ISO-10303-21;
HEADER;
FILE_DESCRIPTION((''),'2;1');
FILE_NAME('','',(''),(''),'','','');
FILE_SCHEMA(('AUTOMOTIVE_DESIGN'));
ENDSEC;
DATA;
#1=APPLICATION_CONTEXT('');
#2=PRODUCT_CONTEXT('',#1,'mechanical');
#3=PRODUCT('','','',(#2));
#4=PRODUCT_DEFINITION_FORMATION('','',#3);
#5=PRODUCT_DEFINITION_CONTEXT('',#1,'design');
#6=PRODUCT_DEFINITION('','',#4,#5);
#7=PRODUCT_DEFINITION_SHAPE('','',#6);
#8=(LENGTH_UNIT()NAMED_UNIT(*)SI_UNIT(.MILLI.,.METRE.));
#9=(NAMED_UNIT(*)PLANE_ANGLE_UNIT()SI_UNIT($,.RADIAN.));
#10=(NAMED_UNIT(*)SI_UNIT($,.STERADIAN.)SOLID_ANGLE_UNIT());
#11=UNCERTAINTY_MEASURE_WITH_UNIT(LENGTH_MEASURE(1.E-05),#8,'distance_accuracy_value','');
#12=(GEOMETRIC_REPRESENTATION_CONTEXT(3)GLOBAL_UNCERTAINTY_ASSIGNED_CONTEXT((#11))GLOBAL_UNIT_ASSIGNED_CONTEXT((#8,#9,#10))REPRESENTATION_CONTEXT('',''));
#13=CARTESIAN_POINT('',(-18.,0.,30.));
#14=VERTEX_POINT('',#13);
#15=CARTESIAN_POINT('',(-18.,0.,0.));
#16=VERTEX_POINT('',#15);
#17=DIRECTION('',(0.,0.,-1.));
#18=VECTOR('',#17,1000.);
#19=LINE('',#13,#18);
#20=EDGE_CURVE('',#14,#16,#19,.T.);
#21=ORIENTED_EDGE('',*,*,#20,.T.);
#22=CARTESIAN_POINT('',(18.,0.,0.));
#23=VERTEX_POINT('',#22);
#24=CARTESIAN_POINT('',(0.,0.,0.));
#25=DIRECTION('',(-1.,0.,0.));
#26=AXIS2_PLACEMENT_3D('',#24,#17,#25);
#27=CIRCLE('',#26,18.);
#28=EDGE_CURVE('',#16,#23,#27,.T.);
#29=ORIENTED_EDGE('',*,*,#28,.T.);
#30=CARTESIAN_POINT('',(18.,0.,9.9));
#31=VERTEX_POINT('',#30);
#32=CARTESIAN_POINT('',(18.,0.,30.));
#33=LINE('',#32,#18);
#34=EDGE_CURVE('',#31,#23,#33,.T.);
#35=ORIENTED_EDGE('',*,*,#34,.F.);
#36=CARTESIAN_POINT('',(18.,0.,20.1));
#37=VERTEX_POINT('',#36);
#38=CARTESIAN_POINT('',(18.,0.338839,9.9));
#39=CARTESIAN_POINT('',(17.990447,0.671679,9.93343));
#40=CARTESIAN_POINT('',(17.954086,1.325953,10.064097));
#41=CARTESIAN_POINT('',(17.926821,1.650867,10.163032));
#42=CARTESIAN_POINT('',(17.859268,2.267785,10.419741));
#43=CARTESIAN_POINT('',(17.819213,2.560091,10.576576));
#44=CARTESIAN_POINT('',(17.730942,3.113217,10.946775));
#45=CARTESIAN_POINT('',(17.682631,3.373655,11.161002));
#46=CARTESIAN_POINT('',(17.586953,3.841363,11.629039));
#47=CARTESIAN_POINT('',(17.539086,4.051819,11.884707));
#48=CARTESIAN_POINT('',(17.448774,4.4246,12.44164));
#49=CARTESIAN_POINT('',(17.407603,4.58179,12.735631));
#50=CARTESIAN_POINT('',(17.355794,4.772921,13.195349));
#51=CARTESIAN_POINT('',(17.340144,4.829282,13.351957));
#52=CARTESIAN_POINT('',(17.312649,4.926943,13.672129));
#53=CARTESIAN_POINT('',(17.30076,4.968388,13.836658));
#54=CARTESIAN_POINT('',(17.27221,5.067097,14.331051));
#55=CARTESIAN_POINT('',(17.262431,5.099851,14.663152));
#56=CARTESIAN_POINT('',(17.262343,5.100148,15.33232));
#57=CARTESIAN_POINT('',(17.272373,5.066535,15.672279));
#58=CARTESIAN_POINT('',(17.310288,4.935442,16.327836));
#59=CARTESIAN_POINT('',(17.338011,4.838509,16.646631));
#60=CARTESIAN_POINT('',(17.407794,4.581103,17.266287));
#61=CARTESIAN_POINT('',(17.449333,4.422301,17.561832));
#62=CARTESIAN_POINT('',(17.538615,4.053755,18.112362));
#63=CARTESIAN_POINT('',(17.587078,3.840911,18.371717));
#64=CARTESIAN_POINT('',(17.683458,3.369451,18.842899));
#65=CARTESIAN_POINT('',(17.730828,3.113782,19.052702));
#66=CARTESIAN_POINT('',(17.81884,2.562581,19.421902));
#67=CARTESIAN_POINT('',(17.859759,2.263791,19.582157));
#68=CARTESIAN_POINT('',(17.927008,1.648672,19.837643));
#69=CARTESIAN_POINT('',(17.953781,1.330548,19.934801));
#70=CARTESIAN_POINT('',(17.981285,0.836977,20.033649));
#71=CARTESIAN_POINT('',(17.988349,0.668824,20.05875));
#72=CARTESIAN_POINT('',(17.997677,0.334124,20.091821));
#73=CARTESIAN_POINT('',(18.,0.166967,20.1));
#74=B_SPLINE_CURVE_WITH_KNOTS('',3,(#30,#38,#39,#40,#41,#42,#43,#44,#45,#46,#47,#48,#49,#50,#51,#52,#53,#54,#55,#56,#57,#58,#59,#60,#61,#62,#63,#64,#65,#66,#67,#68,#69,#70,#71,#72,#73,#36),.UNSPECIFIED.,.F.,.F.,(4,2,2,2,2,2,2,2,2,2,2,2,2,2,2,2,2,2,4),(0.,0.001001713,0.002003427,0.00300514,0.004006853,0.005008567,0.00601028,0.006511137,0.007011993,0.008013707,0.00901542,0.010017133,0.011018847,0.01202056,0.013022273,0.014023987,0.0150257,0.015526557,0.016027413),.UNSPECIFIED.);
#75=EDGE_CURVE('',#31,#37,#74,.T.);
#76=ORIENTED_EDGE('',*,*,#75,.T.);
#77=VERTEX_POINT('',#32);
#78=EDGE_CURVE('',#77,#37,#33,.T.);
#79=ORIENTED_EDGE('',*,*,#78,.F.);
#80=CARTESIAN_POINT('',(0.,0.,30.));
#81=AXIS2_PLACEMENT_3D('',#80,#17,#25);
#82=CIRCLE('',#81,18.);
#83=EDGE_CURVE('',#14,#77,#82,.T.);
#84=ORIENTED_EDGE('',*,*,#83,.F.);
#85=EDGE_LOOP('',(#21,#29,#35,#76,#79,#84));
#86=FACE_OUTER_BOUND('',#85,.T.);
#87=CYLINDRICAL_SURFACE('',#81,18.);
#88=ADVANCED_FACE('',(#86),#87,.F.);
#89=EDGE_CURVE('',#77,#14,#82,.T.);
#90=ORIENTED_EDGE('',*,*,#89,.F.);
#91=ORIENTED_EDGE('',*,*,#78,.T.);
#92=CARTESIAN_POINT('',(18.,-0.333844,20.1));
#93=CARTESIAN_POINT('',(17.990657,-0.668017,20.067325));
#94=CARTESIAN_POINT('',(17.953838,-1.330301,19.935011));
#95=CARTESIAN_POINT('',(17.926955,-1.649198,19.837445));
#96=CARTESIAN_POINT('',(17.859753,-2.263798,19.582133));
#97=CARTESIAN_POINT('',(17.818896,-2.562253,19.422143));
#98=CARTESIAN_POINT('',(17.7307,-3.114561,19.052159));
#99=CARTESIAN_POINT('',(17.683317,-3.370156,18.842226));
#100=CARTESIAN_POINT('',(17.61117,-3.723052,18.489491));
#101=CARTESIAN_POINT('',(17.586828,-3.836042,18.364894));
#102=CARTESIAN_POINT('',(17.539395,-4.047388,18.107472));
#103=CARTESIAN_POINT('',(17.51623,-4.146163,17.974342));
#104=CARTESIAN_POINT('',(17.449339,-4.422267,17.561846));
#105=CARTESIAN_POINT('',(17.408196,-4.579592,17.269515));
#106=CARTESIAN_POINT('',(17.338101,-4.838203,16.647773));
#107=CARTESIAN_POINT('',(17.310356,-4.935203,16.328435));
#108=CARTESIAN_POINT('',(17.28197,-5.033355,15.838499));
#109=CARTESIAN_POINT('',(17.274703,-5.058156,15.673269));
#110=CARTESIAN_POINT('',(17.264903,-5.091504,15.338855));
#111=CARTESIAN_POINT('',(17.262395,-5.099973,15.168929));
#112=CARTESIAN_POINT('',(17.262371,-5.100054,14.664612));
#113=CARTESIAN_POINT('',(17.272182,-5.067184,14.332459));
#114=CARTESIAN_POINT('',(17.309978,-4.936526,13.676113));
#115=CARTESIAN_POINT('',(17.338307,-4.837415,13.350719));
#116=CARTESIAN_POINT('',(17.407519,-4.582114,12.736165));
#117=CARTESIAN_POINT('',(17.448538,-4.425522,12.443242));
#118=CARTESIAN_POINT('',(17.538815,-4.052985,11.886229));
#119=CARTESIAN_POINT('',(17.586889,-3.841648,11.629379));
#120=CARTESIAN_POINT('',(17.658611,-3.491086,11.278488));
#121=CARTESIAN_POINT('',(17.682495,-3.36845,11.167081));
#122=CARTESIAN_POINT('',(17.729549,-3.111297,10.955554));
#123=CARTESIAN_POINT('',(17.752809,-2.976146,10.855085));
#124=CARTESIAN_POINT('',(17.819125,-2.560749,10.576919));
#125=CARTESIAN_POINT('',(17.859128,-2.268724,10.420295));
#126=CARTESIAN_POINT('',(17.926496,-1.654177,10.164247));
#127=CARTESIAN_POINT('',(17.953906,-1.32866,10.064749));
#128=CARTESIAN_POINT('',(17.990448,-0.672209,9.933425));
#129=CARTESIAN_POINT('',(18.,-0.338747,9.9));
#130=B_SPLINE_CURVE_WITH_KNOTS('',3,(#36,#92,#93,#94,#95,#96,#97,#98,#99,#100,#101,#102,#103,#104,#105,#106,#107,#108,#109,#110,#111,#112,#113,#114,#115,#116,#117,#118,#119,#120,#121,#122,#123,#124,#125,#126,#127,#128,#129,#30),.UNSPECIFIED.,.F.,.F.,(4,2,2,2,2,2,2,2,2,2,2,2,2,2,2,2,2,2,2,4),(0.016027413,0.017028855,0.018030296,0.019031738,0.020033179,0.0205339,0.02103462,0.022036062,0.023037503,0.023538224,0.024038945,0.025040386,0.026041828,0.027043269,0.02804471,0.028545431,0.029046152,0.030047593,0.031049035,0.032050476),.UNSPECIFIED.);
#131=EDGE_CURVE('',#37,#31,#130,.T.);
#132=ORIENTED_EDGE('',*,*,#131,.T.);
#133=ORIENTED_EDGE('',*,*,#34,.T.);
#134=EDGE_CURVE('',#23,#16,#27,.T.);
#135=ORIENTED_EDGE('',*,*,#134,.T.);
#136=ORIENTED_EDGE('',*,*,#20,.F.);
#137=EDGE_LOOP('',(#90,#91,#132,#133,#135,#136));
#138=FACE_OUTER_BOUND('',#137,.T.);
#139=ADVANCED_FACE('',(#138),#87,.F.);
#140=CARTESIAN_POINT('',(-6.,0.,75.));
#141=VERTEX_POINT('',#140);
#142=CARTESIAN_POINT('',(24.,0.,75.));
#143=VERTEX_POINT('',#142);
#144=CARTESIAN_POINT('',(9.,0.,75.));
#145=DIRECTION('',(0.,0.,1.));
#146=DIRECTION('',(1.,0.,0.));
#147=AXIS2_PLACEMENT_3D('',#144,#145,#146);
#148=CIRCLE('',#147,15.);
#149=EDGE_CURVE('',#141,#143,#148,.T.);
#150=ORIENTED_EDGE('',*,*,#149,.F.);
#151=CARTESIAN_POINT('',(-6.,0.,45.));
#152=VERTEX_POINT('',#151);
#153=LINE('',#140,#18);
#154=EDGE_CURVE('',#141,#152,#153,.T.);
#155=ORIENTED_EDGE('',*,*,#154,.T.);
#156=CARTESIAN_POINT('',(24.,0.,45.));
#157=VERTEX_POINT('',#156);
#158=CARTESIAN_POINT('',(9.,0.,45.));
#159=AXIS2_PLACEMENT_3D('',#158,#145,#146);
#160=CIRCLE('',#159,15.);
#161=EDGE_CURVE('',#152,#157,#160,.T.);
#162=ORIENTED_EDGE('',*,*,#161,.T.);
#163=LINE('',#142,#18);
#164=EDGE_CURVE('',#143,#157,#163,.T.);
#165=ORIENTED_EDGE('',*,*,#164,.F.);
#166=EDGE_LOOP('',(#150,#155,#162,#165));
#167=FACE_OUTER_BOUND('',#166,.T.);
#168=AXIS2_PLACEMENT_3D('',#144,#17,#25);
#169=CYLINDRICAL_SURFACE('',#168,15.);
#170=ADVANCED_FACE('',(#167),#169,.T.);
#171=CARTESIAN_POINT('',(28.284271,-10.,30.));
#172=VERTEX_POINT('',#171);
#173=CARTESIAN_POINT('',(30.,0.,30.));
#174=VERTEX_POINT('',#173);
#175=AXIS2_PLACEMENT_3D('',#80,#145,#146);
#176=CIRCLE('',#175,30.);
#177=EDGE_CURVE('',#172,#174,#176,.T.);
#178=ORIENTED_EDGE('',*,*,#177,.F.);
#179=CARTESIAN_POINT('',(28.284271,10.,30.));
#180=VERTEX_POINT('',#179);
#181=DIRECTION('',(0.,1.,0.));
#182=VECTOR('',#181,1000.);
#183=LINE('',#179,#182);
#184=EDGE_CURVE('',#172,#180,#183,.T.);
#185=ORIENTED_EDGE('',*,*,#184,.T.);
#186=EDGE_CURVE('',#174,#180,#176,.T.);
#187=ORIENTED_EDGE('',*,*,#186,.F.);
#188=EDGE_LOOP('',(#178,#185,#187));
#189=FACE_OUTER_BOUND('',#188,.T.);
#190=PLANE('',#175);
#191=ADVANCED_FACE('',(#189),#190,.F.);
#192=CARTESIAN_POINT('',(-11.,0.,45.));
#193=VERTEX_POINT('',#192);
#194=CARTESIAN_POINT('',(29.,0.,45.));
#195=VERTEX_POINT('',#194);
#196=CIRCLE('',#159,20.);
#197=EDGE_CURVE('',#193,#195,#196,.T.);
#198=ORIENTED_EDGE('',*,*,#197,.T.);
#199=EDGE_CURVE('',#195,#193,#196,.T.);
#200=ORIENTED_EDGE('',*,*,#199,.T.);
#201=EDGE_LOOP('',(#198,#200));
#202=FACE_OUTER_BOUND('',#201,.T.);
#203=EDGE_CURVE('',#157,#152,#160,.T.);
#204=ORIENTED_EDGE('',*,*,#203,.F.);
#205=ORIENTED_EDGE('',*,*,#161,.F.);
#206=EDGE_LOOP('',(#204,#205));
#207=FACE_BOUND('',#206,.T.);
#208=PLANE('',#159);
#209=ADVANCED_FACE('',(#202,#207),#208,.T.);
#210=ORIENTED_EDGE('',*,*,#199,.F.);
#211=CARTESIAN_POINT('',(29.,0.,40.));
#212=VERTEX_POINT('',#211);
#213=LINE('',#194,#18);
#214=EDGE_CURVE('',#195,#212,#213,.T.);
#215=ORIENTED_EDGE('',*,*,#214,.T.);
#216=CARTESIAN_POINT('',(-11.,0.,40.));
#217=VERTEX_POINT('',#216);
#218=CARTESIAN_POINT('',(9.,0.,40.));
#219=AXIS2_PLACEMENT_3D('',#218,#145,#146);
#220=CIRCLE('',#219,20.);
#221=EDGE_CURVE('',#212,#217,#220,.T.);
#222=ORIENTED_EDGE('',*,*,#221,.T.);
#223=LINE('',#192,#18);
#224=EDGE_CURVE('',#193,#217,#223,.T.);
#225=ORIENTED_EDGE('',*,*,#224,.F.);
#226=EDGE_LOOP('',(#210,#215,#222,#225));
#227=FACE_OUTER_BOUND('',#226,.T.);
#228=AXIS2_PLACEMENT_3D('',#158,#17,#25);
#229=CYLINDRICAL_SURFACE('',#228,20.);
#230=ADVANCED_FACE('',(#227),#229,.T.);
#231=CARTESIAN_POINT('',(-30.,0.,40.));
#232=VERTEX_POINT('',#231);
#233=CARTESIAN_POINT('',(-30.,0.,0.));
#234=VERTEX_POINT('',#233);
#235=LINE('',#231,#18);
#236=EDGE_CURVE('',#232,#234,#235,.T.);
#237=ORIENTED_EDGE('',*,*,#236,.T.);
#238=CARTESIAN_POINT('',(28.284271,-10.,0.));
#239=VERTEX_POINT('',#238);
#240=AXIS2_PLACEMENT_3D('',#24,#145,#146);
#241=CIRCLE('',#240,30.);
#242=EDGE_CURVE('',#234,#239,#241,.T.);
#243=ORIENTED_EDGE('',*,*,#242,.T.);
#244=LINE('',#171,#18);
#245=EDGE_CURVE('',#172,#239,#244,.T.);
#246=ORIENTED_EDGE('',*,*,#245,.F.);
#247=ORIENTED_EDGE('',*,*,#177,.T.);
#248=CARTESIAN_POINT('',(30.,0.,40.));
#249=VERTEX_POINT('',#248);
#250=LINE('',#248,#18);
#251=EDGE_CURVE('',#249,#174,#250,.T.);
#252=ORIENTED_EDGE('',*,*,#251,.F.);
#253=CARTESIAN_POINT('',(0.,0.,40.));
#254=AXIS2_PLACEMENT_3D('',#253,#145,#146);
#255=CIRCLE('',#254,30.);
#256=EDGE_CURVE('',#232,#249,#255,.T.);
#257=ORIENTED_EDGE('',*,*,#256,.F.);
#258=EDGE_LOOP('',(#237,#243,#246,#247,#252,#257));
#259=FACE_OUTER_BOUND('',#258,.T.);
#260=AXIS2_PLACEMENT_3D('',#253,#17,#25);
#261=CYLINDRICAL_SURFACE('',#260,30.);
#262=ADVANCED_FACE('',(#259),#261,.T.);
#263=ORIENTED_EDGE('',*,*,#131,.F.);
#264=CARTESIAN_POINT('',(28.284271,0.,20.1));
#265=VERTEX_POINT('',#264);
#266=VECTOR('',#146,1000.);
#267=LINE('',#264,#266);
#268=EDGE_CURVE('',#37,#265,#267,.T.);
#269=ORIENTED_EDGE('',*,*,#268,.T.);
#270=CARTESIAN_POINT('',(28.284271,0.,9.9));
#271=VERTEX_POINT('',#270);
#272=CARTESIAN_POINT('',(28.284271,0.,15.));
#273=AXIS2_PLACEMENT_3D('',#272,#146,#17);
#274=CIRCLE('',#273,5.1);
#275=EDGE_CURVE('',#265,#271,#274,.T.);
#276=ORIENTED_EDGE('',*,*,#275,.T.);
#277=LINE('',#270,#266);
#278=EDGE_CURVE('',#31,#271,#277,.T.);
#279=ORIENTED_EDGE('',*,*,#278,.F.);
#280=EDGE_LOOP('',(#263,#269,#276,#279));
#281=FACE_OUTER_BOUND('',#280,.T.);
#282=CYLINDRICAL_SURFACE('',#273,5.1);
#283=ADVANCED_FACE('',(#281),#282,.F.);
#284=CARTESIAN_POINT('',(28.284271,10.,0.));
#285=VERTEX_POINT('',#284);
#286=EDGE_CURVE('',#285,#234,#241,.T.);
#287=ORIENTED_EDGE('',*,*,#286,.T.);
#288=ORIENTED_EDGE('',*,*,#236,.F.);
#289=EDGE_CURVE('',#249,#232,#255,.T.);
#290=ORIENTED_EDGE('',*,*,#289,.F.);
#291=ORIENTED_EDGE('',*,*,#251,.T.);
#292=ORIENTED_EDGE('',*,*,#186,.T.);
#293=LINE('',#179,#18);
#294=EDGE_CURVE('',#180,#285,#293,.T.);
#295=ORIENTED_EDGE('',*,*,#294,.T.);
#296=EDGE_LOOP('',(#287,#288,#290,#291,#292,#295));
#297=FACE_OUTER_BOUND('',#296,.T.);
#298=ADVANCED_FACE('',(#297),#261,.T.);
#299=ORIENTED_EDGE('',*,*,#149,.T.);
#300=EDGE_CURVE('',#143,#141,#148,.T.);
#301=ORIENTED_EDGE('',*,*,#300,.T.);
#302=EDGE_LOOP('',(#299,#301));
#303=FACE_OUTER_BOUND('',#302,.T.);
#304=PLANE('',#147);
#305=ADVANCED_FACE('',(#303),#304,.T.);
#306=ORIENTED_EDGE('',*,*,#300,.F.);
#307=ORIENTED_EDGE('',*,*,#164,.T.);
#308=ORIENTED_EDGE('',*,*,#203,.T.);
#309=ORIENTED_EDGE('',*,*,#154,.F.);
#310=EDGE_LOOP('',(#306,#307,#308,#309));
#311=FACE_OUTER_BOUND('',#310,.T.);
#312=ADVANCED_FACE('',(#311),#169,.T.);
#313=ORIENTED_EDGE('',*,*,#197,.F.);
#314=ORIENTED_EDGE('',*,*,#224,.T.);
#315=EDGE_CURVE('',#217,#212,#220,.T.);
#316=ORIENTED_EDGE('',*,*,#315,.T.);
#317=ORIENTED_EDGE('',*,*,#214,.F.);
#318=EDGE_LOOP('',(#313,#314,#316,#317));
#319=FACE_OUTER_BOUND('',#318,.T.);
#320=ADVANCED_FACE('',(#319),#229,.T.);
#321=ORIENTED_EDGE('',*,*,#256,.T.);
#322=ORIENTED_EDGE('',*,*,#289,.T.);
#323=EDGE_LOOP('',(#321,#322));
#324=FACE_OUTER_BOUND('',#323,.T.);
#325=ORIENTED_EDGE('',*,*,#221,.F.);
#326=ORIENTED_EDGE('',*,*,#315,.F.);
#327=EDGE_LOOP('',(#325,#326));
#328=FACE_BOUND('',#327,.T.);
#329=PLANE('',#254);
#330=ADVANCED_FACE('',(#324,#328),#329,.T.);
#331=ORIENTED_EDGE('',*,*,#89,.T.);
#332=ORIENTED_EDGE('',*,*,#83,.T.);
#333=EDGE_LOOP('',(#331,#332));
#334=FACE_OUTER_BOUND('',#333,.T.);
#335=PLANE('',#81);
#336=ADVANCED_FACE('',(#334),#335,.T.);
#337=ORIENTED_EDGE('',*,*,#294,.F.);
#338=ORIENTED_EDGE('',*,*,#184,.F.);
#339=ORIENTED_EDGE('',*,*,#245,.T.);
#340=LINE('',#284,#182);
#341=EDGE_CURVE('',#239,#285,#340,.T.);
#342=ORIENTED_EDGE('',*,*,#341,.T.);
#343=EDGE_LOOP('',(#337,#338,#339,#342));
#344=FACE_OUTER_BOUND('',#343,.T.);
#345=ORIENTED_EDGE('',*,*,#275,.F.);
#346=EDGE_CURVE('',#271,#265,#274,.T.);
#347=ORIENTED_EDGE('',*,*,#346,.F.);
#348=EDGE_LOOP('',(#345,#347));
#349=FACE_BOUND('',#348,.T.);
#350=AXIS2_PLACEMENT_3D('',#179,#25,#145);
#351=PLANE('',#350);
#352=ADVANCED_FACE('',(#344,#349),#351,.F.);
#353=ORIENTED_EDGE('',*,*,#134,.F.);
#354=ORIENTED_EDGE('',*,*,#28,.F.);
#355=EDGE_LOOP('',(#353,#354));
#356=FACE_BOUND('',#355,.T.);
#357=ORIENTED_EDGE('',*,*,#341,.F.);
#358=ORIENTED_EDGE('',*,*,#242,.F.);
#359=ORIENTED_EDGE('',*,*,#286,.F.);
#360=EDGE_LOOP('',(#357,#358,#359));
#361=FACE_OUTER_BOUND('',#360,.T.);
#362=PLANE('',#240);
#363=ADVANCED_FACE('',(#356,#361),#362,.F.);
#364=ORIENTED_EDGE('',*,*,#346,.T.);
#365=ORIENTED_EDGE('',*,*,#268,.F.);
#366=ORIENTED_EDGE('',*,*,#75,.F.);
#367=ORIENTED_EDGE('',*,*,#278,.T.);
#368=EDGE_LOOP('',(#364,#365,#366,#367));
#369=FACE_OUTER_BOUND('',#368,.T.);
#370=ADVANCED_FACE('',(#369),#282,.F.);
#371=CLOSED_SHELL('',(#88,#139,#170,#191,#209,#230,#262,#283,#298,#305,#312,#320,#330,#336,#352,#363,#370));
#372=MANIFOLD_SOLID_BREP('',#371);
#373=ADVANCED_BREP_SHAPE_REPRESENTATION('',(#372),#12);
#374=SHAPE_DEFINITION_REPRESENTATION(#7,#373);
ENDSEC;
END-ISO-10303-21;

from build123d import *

# Parameters (mm, degrees)
SKETCH_1_R              = 30
EXTRUDE_1_DEPTH         = 40
SKETCH_2_R              = 20
EXTRUDE_2_DEPTH         = 5
SKETCH_3_R              = 15
EXTRUDE_3_DEPTH         = 30
SKETCH_5_R              = 18
CUT_EXTRUDE_1_DEPTH     = 30
HOLE_WIZARD_M12_1_D     = 10.2
HOLE_WIZARD_M12_1_DEPTH = 29.25
HOLE_WIZARD_M12_1_TIP   = 3.064389157


with BuildPart() as part:
    # 草图1 → 凸台-拉伸1 (new body)
    with BuildSketch(Plane.XY):
        Circle(SKETCH_1_R)
    extrude(amount=EXTRUDE_1_DEPTH)

    # 草图2 → 凸台-拉伸2 (add)
    with BuildSketch(Plane.XY.offset(40)):
        with Locations((9, 0)):
            Circle(SKETCH_2_R)
    extrude(amount=EXTRUDE_2_DEPTH)

    # 草图3 → 凸台-拉伸3 (add)
    with BuildSketch(Plane.XY.offset(45)):
        with Locations((9, 0)):
            Circle(SKETCH_3_R)
    extrude(amount=EXTRUDE_3_DEPTH)

    # 草图5 → 切除-拉伸1 (cut)
    with BuildSketch(Plane(origin=(0, 0, 0), x_dir=(-1, 0, 0), z_dir=(0, 0, -1))):
        Circle(SKETCH_5_R)
        Polygon((-30.259977001, 10), (-28.284271247, 10), (-28.284271247, -10), (-32.220348536, -10), (-32.220348536, 10), align=None)
    extrude(amount=-CUT_EXTRUDE_1_DEPTH, mode=Mode.SUBTRACT)

    # M12 螺纹孔1
    with Locations(Plane(origin=(28.284271247, 0, 0), x_dir=(0, 0, -1), z_dir=(1, 0, 0))):
        with Locations((-15, 0)):
            Hole(HOLE_WIZARD_M12_1_D / 2, depth=HOLE_WIZARD_M12_1_DEPTH)
            with Locations((0, 0, -(HOLE_WIZARD_M12_1_DEPTH + HOLE_WIZARD_M12_1_TIP / 2))):  # 118° drill point
                Cone(0, HOLE_WIZARD_M12_1_D / 2, HOLE_WIZARD_M12_1_TIP, mode=Mode.SUBTRACT)


solid = part.part
